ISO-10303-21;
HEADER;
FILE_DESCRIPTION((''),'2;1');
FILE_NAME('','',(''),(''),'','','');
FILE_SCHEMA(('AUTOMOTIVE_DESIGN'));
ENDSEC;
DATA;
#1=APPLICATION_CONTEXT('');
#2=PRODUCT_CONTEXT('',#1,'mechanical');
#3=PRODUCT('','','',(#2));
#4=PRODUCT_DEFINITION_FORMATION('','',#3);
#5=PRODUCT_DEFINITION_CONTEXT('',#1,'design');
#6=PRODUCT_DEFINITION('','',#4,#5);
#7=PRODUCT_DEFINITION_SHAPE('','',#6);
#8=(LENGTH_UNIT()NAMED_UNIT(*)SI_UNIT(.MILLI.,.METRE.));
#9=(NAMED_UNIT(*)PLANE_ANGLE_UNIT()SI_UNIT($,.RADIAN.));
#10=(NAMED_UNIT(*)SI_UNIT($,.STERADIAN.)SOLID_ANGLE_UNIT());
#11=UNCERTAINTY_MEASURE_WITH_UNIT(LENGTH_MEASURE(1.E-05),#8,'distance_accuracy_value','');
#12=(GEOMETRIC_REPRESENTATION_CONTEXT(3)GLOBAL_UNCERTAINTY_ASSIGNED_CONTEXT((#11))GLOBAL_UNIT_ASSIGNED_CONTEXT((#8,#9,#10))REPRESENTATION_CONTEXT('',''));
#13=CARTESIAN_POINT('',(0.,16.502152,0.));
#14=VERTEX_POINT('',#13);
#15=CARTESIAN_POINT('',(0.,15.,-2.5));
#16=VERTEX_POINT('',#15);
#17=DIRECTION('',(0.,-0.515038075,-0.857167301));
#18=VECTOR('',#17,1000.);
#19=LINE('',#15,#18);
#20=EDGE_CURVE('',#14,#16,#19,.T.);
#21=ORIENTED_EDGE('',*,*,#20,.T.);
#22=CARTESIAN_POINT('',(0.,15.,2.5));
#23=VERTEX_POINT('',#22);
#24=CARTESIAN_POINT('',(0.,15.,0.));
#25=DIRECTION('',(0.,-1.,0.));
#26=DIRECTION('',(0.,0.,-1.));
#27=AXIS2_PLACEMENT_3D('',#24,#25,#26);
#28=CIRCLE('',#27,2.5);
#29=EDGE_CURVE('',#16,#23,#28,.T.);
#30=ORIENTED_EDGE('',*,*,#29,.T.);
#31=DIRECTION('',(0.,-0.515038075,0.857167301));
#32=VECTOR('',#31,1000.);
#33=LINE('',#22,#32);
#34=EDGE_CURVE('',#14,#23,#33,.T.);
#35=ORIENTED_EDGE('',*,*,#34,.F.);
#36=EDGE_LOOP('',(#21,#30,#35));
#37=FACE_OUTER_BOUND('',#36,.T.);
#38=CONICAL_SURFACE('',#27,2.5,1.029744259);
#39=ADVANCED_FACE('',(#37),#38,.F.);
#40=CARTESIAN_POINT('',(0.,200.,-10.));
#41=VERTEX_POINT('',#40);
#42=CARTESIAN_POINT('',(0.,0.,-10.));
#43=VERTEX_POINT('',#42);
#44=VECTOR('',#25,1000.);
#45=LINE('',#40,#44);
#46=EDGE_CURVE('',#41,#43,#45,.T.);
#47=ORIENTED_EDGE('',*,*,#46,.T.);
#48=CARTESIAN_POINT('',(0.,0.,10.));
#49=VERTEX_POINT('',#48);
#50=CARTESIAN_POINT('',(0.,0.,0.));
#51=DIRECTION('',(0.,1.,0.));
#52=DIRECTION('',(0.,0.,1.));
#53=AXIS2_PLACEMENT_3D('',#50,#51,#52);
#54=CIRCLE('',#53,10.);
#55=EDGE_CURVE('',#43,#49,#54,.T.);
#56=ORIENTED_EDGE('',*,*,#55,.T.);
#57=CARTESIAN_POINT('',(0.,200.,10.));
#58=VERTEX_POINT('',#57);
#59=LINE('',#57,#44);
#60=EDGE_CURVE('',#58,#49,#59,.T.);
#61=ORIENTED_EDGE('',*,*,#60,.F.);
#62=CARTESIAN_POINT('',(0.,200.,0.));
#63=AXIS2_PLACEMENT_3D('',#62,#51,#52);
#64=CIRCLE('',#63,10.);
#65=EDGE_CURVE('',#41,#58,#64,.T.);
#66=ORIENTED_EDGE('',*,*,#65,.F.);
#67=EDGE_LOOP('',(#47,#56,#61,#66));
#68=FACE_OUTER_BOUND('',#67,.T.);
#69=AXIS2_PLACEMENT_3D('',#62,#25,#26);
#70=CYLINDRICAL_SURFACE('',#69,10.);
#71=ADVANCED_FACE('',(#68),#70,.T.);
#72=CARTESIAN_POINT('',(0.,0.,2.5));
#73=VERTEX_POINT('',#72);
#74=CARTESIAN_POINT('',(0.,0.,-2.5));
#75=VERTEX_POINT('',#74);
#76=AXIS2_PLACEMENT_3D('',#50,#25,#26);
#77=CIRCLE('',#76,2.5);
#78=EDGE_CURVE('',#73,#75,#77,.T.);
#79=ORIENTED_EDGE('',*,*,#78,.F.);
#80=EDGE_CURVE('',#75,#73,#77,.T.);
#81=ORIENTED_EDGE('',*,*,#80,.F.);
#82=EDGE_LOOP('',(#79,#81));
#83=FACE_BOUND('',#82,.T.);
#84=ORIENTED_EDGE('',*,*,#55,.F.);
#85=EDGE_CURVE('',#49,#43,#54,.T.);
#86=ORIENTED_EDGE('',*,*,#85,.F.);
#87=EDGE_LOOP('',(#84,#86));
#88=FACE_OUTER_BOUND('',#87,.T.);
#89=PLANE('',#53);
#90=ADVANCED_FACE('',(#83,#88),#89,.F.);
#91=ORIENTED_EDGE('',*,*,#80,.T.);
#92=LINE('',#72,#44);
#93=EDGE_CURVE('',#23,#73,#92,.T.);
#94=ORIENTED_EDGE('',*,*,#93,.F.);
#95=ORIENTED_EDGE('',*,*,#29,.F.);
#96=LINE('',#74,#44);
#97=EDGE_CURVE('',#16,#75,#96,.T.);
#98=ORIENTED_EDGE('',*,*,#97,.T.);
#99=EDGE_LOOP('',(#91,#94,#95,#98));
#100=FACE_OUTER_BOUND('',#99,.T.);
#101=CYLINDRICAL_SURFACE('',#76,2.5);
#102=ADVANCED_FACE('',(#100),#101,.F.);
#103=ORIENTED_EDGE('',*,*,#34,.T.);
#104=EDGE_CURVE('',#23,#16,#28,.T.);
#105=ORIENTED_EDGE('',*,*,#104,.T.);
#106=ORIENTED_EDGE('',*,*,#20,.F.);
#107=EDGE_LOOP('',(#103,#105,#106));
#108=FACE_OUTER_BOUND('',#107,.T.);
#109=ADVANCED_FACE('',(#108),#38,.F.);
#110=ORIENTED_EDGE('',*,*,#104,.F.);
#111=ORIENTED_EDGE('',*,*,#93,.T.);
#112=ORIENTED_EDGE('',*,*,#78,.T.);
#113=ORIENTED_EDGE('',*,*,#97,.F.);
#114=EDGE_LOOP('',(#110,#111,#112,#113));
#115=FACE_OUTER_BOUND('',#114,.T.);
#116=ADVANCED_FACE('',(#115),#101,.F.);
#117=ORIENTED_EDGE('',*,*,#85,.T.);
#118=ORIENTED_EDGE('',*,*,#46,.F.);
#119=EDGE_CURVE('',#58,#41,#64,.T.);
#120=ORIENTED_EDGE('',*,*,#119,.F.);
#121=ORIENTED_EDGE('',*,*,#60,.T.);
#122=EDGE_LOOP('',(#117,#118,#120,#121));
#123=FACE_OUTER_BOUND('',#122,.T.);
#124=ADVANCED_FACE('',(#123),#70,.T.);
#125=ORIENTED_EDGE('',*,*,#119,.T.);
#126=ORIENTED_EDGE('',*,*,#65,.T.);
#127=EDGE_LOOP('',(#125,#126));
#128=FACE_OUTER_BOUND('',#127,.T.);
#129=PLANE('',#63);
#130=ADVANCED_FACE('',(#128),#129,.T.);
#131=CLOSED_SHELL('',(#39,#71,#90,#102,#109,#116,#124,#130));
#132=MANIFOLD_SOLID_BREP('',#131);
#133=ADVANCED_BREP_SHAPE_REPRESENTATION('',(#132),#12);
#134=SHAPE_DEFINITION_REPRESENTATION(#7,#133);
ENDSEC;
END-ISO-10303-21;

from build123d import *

# Parameters (mm, degrees)
SKETCH1_R             = 10
BOSS_EXTRUDE1_DEPTH   = 200
M6_TAPPED_HOLE1_D     = 5
M6_TAPPED_HOLE1_DEPTH = 15
M6_TAPPED_HOLE1_TIP   = 1.502151548


with BuildPart() as part:
    # Sketch1 → Boss-Extrude1 (new body)
    with BuildSketch(Plane(origin=(0, 0, 0), x_dir=(1, 0, 0), z_dir=(0, 1, 0))):
        with Locations(Location((0, 0, 0), (0, 0, 270))):
            Circle(SKETCH1_R)
    extrude(amount=BOSS_EXTRUDE1_DEPTH)

    # M6 Tapped Hole1
    with Locations(Plane(origin=(0, 0, 0), x_dir=(-1, 0, 0), z_dir=(0, -1, 0))):
        with Locations((0, 0)):
            Hole(M6_TAPPED_HOLE1_D / 2, depth=M6_TAPPED_HOLE1_DEPTH)
            with Locations((0, 0, -(M6_TAPPED_HOLE1_DEPTH + M6_TAPPED_HOLE1_TIP / 2))):  # 118° drill point
                Cone(0, M6_TAPPED_HOLE1_D / 2, M6_TAPPED_HOLE1_TIP, mode=Mode.SUBTRACT)


solid = part.part
